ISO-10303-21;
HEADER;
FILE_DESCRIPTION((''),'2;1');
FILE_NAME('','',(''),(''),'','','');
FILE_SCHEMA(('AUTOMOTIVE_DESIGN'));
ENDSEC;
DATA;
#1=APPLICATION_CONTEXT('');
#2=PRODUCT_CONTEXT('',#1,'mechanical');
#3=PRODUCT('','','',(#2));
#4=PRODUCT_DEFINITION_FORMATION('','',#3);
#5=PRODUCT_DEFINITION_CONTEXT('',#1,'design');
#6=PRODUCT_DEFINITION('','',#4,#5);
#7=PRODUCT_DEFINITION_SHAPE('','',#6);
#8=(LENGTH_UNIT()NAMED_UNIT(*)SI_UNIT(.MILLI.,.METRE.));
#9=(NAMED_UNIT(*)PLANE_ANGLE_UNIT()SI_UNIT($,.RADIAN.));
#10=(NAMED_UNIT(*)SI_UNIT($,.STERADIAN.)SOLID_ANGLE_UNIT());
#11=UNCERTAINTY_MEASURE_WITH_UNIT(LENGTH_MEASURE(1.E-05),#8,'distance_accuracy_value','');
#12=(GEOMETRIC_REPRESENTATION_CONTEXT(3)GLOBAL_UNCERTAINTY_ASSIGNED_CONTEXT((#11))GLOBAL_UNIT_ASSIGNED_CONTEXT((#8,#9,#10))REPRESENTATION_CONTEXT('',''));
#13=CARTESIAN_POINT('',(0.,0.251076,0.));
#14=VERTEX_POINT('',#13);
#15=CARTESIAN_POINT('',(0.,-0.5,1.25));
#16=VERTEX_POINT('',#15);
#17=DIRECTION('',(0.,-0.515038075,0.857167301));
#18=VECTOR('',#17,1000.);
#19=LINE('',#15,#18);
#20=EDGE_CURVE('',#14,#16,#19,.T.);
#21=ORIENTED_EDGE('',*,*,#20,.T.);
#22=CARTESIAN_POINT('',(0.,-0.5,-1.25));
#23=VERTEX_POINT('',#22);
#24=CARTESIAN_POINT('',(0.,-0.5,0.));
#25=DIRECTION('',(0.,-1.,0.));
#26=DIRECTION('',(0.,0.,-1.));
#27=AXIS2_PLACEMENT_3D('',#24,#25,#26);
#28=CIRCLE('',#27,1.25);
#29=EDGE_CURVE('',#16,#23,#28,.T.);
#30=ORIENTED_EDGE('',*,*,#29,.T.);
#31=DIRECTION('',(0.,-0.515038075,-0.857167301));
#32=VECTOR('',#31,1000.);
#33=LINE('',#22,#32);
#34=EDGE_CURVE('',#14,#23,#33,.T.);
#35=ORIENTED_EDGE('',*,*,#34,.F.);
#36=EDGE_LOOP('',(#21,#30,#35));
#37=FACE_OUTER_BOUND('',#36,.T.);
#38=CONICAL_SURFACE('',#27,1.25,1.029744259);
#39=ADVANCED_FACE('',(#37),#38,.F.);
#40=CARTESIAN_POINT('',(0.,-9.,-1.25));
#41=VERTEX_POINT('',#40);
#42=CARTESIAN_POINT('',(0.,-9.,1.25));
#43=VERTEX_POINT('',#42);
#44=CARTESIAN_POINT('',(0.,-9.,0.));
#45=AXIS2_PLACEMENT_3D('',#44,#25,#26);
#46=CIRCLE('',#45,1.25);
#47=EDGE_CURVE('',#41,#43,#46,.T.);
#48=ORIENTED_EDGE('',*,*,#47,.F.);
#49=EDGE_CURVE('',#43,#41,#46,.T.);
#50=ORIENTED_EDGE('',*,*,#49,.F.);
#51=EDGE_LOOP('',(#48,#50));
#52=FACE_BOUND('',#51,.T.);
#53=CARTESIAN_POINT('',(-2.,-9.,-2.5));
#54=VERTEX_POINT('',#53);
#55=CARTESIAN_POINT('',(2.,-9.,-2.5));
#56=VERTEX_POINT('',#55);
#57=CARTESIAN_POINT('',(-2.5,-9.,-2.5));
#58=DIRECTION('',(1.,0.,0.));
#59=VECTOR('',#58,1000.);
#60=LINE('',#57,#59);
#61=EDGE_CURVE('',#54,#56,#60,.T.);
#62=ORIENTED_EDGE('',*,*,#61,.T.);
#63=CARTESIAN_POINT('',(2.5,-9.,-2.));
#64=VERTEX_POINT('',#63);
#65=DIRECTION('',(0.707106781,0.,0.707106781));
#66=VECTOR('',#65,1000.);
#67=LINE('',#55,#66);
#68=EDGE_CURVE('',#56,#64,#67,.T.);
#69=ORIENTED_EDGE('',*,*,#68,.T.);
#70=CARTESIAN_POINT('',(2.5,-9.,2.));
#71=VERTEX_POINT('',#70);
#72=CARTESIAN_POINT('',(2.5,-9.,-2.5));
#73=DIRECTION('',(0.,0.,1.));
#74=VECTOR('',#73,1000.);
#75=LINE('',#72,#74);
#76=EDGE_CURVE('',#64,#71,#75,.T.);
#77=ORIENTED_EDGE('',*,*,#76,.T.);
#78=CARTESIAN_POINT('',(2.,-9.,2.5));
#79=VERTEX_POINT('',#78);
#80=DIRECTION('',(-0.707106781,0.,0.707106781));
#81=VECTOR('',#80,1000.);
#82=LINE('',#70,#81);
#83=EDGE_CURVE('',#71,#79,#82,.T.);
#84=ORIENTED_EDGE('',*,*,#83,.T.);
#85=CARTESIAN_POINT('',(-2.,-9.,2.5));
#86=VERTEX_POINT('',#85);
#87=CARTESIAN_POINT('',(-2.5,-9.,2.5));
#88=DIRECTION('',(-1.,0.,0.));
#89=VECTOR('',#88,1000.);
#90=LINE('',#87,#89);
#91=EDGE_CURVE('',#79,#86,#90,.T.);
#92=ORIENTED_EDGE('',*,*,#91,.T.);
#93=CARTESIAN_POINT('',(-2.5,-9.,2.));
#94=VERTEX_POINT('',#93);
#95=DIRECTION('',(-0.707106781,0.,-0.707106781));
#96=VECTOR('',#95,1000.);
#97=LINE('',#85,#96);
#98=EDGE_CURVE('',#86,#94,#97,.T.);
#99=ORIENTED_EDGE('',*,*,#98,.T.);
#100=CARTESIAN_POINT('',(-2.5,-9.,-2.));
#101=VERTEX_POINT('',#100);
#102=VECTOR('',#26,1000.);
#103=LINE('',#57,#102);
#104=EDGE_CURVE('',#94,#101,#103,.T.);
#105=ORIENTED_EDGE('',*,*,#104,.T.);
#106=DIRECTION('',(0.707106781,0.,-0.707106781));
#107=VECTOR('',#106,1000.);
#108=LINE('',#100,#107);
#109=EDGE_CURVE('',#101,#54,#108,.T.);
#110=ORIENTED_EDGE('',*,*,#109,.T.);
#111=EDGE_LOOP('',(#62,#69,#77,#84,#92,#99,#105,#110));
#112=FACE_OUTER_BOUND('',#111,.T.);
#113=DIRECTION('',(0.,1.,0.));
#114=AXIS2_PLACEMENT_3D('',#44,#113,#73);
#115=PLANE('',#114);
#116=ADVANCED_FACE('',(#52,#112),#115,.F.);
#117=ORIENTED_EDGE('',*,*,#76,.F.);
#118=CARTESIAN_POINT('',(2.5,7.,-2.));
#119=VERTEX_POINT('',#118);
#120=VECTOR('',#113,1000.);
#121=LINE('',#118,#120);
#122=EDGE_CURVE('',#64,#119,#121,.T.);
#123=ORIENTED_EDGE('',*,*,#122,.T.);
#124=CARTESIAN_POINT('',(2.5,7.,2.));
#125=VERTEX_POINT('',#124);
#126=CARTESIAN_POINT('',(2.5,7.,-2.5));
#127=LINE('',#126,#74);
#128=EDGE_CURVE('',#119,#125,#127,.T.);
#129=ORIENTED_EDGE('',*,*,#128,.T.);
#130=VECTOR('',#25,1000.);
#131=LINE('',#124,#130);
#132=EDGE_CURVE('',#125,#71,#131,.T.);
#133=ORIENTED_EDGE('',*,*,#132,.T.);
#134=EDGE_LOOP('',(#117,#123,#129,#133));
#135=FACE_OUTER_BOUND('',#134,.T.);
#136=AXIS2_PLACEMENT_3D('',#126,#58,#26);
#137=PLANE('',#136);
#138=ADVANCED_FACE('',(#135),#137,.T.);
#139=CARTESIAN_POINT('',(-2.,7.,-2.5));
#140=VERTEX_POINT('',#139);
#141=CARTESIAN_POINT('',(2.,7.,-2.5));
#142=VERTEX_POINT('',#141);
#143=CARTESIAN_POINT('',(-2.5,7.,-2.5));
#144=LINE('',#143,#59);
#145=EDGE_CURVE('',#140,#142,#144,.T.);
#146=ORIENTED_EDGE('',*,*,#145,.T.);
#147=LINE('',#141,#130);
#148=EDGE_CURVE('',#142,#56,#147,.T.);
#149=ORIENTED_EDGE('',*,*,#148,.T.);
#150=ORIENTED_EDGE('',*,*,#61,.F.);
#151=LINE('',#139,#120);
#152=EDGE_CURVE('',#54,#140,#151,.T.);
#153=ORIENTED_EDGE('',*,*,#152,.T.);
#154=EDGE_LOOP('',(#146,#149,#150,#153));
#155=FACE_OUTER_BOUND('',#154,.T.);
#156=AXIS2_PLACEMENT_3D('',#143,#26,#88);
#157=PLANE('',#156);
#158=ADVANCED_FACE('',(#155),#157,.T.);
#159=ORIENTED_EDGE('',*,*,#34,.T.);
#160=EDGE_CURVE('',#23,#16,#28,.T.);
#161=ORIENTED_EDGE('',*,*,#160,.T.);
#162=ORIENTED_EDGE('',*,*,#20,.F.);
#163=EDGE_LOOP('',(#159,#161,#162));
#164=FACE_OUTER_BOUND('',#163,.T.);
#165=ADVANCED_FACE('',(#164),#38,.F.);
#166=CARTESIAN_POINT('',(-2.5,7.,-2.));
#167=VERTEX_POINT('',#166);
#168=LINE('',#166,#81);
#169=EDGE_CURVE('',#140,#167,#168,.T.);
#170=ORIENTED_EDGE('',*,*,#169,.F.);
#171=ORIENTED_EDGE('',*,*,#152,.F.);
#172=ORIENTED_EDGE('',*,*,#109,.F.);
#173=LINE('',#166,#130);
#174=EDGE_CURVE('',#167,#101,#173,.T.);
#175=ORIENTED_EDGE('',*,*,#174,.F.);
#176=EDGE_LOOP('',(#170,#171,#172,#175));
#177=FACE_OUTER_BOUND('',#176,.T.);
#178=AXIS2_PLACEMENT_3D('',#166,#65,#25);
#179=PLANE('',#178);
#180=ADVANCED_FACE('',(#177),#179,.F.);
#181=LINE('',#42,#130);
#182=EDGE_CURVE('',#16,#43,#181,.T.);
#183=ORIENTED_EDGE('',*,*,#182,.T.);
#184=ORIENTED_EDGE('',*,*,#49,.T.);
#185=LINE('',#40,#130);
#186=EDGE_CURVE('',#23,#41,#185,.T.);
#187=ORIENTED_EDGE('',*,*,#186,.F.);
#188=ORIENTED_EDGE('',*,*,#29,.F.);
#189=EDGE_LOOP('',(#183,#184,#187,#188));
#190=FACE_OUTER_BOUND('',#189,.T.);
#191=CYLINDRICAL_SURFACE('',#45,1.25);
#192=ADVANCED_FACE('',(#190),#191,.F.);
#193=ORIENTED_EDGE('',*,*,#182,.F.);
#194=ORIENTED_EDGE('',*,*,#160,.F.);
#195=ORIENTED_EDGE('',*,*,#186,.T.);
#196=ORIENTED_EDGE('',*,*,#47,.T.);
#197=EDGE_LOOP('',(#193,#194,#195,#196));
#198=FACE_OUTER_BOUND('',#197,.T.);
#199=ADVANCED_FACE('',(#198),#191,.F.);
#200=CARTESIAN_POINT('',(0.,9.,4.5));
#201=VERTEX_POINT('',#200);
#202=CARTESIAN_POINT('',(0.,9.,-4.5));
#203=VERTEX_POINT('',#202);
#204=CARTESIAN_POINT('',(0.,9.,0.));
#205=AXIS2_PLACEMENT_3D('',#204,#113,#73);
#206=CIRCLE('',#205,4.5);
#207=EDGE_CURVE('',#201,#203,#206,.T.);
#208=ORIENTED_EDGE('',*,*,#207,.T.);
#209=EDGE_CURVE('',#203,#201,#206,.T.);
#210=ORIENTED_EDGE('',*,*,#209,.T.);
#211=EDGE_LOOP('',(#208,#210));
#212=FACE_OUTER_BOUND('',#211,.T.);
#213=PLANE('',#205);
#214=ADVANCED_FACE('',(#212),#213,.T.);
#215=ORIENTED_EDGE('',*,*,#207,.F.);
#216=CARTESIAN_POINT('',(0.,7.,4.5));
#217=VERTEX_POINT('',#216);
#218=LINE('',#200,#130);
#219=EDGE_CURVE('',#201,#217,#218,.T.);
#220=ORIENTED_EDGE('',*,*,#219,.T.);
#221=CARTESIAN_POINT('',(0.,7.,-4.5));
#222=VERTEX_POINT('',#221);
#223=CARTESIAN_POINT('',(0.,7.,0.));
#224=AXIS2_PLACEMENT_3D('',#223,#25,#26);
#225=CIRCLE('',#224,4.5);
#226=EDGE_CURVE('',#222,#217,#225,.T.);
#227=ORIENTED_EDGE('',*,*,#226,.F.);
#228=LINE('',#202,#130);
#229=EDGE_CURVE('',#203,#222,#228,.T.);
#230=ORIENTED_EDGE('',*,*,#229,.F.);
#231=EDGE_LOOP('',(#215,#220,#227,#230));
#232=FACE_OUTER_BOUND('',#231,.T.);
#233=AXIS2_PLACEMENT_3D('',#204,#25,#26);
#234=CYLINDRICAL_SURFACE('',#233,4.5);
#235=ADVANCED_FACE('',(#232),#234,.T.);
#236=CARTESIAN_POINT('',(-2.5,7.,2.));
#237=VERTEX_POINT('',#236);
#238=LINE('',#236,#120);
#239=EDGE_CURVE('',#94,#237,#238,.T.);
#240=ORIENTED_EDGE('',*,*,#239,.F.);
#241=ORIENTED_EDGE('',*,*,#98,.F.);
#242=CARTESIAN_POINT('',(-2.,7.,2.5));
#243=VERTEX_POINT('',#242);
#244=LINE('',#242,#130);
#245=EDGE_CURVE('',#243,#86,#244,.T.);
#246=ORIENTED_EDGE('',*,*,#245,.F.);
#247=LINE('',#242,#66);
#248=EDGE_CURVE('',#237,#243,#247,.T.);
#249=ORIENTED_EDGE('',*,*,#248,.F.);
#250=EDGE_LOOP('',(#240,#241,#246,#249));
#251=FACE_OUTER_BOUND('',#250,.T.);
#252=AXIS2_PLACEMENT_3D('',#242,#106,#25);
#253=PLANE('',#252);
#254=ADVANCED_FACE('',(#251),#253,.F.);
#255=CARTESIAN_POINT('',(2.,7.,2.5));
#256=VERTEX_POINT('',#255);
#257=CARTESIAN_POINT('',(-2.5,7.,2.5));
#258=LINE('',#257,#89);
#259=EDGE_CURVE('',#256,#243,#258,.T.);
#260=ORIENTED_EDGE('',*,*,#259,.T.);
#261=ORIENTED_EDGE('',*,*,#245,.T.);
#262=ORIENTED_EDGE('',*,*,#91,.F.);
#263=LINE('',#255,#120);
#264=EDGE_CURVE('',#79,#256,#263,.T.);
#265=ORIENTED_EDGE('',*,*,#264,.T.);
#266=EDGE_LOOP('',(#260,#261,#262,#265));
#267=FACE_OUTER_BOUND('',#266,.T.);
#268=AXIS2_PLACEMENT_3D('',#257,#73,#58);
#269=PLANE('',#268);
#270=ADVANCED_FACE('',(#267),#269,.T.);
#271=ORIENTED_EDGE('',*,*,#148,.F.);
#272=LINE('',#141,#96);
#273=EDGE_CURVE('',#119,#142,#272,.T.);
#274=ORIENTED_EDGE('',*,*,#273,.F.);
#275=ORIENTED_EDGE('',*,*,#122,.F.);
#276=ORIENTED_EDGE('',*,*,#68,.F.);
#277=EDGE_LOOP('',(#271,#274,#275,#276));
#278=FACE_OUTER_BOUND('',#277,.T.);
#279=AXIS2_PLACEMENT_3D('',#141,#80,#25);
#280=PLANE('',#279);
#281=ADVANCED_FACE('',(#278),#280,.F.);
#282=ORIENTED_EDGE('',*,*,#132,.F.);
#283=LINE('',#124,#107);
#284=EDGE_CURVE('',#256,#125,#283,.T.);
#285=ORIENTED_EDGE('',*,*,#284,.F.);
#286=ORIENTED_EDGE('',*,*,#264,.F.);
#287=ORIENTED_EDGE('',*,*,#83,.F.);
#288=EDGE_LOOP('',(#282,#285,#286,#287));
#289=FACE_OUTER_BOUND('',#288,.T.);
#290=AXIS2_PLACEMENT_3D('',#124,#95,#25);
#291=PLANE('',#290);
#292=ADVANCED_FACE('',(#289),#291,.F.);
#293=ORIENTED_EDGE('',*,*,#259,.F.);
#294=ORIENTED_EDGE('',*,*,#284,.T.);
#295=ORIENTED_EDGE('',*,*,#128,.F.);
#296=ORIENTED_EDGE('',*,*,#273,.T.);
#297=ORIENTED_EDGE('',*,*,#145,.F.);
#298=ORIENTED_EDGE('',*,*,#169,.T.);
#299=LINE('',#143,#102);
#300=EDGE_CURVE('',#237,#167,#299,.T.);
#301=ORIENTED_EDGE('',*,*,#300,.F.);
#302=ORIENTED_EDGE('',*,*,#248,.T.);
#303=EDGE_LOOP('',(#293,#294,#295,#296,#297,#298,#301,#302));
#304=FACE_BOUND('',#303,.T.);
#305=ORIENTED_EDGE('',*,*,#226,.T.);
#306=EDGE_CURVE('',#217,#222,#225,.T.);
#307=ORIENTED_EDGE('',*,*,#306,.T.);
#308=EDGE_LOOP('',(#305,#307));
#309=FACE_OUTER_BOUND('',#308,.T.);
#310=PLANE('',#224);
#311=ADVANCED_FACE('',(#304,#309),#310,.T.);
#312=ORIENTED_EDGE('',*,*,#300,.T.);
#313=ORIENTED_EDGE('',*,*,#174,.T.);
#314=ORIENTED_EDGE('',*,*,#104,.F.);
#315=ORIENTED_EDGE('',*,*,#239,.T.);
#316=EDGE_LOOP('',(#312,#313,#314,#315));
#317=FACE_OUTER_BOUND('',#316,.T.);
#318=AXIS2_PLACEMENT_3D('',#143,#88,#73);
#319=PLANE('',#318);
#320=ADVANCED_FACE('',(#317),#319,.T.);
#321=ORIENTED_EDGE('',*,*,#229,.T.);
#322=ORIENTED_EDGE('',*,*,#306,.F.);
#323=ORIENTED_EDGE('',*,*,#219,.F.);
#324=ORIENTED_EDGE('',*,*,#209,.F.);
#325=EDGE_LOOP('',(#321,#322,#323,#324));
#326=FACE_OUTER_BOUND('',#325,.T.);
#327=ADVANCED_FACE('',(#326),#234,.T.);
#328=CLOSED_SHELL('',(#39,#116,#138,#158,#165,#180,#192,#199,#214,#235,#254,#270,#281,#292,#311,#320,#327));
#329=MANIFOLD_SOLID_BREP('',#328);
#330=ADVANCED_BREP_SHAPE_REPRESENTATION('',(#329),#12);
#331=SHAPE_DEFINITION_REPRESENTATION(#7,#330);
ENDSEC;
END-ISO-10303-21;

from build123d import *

# Parameters (mm, degrees)
SKETCH_1_R             = 4.5
EXTRUDE_1_DEPTH        = 9
CUT_EXTRUDE_START      = -16
SKETCH_2_R             = 4.5
SKETCH_2_W             = 5
SKETCH_2_H             = 5
CUT_EXTRUDE_1_DEPTH    = 16
HOLE_WIZARD_M3_1_D     = 2.5
HOLE_WIZARD_M3_1_DEPTH = 8.5
HOLE_WIZARD_M3_1_TIP   = 0.751075774
CHAMFER_1_SIZE         = 0.5


with BuildPart() as part:
    # 草图1 → 凸台-拉伸1 (new, symmetric)
    with BuildSketch(Plane(origin=(0, 0, 0), x_dir=(1, 0, 0), z_dir=(0, 1, 0))):
        with Locations(Location((0, 0, 0), (0, 0, 270))):
            Circle(SKETCH_1_R)
    extrude(amount=EXTRUDE_1_DEPTH, both=True)

    # 草图2 → 切除-拉伸1 (cut)
    with BuildSketch(Plane.XZ.offset(9).offset(CUT_EXTRUDE_START)):
        with Locations(Location((0, 0, 0), (0, 0, 270))):
            Circle(SKETCH_2_R)
        Rectangle(SKETCH_2_W, SKETCH_2_H, mode=Mode.SUBTRACT)
    extrude(amount=CUT_EXTRUDE_1_DEPTH, mode=Mode.SUBTRACT)

    # M3 螺纹孔1
    with Locations(Plane(origin=(0, -9, 0), x_dir=(-1, 0, 0), z_dir=(0, -1, 0))):
        with Locations((0, 0)):
            Hole(HOLE_WIZARD_M3_1_D / 2, depth=HOLE_WIZARD_M3_1_DEPTH)
            with Locations((0, 0, -(HOLE_WIZARD_M3_1_DEPTH + HOLE_WIZARD_M3_1_TIP / 2))):  # 118° drill point
                Cone(0, HOLE_WIZARD_M3_1_D / 2, HOLE_WIZARD_M3_1_TIP, mode=Mode.SUBTRACT)

    # 倒角1
    chamfer_1_edges = [part.edges().sort_by_distance(p)[0] for p in [
        (2.5, -1, -2.5),
        (-2.5, -1, -2.5),
        (-2.5, -1, 2.5),
        (2.5, -1, 2.5),
    ]]
    chamfer(chamfer_1_edges, length=CHAMFER_1_SIZE)


solid = part.part
